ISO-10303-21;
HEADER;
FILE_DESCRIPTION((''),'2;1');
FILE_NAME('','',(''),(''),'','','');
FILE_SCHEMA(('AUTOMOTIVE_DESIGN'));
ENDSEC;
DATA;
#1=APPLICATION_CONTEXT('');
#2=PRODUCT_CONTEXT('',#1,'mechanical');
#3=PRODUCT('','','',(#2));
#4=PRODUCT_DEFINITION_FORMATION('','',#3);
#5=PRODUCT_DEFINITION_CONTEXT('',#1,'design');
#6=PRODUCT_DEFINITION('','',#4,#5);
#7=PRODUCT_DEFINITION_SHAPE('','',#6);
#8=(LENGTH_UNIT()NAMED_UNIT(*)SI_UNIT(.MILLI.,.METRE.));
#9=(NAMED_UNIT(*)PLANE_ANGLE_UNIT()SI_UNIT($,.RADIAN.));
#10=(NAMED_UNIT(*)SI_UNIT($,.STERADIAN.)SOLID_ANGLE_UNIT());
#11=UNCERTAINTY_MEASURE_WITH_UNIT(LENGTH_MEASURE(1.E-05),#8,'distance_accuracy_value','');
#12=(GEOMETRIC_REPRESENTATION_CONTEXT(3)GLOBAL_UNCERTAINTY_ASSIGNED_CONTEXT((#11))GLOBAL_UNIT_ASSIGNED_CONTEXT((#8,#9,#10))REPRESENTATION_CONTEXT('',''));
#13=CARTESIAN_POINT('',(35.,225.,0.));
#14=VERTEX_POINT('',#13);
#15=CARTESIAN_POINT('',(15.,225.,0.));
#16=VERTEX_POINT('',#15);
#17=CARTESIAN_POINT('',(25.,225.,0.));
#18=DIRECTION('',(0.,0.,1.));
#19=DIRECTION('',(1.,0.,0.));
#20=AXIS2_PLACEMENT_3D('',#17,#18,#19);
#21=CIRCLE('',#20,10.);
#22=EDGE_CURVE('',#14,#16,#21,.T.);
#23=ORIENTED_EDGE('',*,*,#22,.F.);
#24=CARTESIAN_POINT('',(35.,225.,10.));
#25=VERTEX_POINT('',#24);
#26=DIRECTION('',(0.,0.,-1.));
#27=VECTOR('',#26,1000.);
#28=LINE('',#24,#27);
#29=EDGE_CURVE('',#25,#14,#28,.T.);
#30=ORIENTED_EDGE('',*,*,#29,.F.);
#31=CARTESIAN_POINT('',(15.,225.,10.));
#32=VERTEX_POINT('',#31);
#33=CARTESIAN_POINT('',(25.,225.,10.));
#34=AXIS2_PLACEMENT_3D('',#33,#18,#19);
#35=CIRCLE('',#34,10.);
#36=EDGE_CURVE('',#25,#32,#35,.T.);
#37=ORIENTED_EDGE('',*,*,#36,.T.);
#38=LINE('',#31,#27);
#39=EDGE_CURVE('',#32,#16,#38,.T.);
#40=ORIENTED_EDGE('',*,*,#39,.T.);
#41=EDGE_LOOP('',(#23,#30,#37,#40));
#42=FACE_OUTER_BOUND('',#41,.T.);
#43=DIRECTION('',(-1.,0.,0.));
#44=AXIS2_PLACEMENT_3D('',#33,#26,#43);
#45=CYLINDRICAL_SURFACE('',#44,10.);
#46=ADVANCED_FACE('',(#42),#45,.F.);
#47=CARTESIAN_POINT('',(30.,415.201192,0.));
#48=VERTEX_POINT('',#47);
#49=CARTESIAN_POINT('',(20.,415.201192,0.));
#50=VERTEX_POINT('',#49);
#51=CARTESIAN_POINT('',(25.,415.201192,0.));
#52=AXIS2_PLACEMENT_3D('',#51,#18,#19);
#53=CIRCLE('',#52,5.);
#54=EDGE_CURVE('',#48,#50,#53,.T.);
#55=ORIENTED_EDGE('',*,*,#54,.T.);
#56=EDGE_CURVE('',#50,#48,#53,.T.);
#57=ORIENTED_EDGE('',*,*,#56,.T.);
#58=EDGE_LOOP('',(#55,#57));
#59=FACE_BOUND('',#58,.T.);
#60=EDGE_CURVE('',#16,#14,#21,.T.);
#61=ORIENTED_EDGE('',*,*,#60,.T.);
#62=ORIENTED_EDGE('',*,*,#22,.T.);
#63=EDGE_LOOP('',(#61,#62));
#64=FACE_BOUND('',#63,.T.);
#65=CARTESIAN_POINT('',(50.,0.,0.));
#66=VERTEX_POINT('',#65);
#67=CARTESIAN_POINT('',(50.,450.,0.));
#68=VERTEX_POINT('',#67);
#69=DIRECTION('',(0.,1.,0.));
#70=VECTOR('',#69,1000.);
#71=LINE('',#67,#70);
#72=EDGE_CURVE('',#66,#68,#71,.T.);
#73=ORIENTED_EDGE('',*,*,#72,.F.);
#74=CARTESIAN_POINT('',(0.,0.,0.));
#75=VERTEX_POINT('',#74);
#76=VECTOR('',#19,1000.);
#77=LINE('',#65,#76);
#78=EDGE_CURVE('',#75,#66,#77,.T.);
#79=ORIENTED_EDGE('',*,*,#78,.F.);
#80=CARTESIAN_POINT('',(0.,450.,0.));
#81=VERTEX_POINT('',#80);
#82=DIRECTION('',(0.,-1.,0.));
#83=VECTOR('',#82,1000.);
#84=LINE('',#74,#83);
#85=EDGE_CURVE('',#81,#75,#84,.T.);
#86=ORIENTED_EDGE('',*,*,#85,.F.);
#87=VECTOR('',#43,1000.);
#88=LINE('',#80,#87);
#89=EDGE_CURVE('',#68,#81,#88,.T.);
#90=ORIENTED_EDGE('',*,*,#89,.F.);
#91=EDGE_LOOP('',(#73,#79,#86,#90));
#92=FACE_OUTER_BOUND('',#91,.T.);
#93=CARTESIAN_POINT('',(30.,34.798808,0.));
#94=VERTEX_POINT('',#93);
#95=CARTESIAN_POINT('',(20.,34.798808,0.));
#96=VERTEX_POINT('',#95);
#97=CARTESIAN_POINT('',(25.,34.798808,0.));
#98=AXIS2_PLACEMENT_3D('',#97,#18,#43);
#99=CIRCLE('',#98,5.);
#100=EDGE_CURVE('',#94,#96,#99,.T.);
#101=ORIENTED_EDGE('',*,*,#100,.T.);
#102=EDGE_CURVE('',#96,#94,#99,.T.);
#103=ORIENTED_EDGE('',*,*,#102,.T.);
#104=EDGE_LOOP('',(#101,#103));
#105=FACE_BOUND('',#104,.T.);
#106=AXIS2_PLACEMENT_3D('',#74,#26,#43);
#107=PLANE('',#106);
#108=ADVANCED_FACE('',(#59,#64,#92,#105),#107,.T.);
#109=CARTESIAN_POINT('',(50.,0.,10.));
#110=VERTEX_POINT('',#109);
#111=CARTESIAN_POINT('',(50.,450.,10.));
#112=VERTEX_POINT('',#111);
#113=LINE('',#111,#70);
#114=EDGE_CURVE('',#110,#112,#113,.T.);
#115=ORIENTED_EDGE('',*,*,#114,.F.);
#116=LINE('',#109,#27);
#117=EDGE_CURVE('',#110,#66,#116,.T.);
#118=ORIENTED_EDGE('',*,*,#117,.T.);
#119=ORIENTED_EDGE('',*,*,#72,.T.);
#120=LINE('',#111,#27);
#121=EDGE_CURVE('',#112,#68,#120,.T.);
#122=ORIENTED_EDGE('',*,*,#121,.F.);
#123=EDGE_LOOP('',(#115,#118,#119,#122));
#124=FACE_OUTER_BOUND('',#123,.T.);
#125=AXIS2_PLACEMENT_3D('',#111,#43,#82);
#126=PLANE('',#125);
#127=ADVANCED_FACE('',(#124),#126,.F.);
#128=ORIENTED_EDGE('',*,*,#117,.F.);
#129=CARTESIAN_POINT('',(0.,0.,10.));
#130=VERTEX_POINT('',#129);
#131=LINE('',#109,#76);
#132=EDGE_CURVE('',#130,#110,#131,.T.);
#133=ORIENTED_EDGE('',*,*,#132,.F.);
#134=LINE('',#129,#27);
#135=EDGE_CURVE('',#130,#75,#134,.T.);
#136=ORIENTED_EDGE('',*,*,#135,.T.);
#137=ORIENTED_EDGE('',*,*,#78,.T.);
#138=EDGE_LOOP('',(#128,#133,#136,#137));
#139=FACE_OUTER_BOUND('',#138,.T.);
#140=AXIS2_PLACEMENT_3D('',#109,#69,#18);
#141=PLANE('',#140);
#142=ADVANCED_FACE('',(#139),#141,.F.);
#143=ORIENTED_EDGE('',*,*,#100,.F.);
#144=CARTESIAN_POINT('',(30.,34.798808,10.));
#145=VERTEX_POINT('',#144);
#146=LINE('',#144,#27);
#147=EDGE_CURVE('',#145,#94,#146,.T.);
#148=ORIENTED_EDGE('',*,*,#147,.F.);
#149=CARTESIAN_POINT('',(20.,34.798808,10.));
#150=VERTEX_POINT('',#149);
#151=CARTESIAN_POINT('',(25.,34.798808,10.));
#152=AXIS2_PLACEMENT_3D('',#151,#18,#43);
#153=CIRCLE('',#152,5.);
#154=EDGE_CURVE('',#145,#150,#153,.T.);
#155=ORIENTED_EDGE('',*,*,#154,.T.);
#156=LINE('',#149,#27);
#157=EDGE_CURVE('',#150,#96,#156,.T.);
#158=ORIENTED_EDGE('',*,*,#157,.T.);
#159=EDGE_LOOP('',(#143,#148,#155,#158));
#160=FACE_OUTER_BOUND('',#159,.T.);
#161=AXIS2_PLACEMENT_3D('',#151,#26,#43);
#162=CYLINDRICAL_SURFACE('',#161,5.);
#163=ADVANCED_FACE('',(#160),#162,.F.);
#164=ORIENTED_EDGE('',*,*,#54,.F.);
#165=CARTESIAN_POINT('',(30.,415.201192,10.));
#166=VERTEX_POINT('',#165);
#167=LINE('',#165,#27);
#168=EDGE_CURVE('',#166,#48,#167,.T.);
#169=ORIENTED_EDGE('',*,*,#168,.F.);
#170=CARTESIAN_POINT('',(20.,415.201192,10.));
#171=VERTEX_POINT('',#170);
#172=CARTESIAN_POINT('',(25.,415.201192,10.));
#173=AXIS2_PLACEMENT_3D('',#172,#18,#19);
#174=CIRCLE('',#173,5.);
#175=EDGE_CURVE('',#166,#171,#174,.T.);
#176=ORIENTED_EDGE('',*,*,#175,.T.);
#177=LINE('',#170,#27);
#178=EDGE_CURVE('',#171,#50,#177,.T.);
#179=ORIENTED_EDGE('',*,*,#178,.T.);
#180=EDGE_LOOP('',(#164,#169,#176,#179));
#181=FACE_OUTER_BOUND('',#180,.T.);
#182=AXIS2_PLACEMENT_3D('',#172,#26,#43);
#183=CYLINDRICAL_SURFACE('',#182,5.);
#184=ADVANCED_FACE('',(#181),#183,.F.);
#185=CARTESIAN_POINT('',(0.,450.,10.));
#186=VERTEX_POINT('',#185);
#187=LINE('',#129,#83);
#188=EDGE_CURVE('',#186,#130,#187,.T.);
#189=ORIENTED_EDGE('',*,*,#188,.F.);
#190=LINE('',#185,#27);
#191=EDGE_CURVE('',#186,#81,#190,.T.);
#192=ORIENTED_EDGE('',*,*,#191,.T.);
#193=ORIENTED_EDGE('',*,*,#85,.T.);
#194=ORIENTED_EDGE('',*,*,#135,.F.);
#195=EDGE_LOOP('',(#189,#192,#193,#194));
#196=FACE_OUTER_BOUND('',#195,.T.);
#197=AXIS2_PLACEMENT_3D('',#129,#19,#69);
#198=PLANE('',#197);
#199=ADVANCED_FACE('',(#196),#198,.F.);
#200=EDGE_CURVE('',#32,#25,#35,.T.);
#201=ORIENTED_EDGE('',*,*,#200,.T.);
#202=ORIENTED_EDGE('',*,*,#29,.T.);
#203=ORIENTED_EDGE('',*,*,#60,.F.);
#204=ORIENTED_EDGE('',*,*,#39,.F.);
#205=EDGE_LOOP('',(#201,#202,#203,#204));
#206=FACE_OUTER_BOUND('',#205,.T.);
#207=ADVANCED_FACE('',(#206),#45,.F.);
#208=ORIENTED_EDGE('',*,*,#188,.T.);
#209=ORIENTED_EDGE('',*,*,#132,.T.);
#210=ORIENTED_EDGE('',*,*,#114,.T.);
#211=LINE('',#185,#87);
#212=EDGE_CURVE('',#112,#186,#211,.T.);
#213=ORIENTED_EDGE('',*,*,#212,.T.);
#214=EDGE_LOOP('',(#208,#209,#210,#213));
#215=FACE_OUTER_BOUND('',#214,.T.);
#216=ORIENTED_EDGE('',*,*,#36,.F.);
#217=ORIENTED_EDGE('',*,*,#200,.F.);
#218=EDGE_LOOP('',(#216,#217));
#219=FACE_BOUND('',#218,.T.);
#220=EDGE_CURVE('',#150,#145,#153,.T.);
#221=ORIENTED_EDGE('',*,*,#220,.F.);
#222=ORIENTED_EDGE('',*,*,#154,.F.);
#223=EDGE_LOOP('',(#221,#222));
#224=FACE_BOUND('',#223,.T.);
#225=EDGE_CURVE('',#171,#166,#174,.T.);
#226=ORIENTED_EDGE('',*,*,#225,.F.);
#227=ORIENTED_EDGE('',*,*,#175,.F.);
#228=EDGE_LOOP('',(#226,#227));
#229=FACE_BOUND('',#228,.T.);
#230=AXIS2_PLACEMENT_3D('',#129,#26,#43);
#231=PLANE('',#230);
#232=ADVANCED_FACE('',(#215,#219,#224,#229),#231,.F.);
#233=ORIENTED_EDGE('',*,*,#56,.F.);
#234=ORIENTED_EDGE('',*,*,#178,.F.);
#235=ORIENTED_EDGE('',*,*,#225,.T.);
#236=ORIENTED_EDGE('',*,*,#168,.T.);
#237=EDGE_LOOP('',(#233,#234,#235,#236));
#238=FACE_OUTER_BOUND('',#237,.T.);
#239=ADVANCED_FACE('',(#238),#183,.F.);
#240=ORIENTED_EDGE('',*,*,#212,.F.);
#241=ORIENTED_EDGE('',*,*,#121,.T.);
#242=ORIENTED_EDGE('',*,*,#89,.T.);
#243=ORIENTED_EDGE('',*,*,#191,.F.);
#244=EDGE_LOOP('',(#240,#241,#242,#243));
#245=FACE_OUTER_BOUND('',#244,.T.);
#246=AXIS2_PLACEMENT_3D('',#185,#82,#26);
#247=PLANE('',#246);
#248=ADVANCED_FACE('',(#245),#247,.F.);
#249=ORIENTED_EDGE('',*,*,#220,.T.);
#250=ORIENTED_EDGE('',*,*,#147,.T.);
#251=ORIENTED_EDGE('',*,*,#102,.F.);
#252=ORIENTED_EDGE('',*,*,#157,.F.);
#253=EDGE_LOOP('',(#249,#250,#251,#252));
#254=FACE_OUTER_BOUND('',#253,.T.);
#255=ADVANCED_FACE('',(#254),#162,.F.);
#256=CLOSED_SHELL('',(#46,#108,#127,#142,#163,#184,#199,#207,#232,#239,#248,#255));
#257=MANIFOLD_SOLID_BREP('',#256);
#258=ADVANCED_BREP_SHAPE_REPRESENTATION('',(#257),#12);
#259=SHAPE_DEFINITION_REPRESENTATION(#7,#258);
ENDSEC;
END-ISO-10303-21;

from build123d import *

# Parameters (mm, degrees)
SKETCH_1_W      = 50
SKETCH_1_H      = 450
SKETCH_1_R      = 10
SKETCH_1_R_2    = 5
EXTRUDE_1_DEPTH = 10


with BuildPart() as part:
    # 草图1 → 凸台-拉伸1 (new body)
    with BuildSketch(Plane.XY):
        with Locations((25, 225)):
            Rectangle(SKETCH_1_W, SKETCH_1_H)
        with Locations((25, 225)):
            Circle(SKETCH_1_R, mode=Mode.SUBTRACT)
        with Locations((25, 415.201191985)):
            Circle(SKETCH_1_R_2, mode=Mode.SUBTRACT)
        with Locations(Location((25, 34.798808015, 0), (0, 0, 180))):
            Circle(SKETCH_1_R_2, mode=Mode.SUBTRACT)
    extrude(amount=EXTRUDE_1_DEPTH)


solid = part.part
